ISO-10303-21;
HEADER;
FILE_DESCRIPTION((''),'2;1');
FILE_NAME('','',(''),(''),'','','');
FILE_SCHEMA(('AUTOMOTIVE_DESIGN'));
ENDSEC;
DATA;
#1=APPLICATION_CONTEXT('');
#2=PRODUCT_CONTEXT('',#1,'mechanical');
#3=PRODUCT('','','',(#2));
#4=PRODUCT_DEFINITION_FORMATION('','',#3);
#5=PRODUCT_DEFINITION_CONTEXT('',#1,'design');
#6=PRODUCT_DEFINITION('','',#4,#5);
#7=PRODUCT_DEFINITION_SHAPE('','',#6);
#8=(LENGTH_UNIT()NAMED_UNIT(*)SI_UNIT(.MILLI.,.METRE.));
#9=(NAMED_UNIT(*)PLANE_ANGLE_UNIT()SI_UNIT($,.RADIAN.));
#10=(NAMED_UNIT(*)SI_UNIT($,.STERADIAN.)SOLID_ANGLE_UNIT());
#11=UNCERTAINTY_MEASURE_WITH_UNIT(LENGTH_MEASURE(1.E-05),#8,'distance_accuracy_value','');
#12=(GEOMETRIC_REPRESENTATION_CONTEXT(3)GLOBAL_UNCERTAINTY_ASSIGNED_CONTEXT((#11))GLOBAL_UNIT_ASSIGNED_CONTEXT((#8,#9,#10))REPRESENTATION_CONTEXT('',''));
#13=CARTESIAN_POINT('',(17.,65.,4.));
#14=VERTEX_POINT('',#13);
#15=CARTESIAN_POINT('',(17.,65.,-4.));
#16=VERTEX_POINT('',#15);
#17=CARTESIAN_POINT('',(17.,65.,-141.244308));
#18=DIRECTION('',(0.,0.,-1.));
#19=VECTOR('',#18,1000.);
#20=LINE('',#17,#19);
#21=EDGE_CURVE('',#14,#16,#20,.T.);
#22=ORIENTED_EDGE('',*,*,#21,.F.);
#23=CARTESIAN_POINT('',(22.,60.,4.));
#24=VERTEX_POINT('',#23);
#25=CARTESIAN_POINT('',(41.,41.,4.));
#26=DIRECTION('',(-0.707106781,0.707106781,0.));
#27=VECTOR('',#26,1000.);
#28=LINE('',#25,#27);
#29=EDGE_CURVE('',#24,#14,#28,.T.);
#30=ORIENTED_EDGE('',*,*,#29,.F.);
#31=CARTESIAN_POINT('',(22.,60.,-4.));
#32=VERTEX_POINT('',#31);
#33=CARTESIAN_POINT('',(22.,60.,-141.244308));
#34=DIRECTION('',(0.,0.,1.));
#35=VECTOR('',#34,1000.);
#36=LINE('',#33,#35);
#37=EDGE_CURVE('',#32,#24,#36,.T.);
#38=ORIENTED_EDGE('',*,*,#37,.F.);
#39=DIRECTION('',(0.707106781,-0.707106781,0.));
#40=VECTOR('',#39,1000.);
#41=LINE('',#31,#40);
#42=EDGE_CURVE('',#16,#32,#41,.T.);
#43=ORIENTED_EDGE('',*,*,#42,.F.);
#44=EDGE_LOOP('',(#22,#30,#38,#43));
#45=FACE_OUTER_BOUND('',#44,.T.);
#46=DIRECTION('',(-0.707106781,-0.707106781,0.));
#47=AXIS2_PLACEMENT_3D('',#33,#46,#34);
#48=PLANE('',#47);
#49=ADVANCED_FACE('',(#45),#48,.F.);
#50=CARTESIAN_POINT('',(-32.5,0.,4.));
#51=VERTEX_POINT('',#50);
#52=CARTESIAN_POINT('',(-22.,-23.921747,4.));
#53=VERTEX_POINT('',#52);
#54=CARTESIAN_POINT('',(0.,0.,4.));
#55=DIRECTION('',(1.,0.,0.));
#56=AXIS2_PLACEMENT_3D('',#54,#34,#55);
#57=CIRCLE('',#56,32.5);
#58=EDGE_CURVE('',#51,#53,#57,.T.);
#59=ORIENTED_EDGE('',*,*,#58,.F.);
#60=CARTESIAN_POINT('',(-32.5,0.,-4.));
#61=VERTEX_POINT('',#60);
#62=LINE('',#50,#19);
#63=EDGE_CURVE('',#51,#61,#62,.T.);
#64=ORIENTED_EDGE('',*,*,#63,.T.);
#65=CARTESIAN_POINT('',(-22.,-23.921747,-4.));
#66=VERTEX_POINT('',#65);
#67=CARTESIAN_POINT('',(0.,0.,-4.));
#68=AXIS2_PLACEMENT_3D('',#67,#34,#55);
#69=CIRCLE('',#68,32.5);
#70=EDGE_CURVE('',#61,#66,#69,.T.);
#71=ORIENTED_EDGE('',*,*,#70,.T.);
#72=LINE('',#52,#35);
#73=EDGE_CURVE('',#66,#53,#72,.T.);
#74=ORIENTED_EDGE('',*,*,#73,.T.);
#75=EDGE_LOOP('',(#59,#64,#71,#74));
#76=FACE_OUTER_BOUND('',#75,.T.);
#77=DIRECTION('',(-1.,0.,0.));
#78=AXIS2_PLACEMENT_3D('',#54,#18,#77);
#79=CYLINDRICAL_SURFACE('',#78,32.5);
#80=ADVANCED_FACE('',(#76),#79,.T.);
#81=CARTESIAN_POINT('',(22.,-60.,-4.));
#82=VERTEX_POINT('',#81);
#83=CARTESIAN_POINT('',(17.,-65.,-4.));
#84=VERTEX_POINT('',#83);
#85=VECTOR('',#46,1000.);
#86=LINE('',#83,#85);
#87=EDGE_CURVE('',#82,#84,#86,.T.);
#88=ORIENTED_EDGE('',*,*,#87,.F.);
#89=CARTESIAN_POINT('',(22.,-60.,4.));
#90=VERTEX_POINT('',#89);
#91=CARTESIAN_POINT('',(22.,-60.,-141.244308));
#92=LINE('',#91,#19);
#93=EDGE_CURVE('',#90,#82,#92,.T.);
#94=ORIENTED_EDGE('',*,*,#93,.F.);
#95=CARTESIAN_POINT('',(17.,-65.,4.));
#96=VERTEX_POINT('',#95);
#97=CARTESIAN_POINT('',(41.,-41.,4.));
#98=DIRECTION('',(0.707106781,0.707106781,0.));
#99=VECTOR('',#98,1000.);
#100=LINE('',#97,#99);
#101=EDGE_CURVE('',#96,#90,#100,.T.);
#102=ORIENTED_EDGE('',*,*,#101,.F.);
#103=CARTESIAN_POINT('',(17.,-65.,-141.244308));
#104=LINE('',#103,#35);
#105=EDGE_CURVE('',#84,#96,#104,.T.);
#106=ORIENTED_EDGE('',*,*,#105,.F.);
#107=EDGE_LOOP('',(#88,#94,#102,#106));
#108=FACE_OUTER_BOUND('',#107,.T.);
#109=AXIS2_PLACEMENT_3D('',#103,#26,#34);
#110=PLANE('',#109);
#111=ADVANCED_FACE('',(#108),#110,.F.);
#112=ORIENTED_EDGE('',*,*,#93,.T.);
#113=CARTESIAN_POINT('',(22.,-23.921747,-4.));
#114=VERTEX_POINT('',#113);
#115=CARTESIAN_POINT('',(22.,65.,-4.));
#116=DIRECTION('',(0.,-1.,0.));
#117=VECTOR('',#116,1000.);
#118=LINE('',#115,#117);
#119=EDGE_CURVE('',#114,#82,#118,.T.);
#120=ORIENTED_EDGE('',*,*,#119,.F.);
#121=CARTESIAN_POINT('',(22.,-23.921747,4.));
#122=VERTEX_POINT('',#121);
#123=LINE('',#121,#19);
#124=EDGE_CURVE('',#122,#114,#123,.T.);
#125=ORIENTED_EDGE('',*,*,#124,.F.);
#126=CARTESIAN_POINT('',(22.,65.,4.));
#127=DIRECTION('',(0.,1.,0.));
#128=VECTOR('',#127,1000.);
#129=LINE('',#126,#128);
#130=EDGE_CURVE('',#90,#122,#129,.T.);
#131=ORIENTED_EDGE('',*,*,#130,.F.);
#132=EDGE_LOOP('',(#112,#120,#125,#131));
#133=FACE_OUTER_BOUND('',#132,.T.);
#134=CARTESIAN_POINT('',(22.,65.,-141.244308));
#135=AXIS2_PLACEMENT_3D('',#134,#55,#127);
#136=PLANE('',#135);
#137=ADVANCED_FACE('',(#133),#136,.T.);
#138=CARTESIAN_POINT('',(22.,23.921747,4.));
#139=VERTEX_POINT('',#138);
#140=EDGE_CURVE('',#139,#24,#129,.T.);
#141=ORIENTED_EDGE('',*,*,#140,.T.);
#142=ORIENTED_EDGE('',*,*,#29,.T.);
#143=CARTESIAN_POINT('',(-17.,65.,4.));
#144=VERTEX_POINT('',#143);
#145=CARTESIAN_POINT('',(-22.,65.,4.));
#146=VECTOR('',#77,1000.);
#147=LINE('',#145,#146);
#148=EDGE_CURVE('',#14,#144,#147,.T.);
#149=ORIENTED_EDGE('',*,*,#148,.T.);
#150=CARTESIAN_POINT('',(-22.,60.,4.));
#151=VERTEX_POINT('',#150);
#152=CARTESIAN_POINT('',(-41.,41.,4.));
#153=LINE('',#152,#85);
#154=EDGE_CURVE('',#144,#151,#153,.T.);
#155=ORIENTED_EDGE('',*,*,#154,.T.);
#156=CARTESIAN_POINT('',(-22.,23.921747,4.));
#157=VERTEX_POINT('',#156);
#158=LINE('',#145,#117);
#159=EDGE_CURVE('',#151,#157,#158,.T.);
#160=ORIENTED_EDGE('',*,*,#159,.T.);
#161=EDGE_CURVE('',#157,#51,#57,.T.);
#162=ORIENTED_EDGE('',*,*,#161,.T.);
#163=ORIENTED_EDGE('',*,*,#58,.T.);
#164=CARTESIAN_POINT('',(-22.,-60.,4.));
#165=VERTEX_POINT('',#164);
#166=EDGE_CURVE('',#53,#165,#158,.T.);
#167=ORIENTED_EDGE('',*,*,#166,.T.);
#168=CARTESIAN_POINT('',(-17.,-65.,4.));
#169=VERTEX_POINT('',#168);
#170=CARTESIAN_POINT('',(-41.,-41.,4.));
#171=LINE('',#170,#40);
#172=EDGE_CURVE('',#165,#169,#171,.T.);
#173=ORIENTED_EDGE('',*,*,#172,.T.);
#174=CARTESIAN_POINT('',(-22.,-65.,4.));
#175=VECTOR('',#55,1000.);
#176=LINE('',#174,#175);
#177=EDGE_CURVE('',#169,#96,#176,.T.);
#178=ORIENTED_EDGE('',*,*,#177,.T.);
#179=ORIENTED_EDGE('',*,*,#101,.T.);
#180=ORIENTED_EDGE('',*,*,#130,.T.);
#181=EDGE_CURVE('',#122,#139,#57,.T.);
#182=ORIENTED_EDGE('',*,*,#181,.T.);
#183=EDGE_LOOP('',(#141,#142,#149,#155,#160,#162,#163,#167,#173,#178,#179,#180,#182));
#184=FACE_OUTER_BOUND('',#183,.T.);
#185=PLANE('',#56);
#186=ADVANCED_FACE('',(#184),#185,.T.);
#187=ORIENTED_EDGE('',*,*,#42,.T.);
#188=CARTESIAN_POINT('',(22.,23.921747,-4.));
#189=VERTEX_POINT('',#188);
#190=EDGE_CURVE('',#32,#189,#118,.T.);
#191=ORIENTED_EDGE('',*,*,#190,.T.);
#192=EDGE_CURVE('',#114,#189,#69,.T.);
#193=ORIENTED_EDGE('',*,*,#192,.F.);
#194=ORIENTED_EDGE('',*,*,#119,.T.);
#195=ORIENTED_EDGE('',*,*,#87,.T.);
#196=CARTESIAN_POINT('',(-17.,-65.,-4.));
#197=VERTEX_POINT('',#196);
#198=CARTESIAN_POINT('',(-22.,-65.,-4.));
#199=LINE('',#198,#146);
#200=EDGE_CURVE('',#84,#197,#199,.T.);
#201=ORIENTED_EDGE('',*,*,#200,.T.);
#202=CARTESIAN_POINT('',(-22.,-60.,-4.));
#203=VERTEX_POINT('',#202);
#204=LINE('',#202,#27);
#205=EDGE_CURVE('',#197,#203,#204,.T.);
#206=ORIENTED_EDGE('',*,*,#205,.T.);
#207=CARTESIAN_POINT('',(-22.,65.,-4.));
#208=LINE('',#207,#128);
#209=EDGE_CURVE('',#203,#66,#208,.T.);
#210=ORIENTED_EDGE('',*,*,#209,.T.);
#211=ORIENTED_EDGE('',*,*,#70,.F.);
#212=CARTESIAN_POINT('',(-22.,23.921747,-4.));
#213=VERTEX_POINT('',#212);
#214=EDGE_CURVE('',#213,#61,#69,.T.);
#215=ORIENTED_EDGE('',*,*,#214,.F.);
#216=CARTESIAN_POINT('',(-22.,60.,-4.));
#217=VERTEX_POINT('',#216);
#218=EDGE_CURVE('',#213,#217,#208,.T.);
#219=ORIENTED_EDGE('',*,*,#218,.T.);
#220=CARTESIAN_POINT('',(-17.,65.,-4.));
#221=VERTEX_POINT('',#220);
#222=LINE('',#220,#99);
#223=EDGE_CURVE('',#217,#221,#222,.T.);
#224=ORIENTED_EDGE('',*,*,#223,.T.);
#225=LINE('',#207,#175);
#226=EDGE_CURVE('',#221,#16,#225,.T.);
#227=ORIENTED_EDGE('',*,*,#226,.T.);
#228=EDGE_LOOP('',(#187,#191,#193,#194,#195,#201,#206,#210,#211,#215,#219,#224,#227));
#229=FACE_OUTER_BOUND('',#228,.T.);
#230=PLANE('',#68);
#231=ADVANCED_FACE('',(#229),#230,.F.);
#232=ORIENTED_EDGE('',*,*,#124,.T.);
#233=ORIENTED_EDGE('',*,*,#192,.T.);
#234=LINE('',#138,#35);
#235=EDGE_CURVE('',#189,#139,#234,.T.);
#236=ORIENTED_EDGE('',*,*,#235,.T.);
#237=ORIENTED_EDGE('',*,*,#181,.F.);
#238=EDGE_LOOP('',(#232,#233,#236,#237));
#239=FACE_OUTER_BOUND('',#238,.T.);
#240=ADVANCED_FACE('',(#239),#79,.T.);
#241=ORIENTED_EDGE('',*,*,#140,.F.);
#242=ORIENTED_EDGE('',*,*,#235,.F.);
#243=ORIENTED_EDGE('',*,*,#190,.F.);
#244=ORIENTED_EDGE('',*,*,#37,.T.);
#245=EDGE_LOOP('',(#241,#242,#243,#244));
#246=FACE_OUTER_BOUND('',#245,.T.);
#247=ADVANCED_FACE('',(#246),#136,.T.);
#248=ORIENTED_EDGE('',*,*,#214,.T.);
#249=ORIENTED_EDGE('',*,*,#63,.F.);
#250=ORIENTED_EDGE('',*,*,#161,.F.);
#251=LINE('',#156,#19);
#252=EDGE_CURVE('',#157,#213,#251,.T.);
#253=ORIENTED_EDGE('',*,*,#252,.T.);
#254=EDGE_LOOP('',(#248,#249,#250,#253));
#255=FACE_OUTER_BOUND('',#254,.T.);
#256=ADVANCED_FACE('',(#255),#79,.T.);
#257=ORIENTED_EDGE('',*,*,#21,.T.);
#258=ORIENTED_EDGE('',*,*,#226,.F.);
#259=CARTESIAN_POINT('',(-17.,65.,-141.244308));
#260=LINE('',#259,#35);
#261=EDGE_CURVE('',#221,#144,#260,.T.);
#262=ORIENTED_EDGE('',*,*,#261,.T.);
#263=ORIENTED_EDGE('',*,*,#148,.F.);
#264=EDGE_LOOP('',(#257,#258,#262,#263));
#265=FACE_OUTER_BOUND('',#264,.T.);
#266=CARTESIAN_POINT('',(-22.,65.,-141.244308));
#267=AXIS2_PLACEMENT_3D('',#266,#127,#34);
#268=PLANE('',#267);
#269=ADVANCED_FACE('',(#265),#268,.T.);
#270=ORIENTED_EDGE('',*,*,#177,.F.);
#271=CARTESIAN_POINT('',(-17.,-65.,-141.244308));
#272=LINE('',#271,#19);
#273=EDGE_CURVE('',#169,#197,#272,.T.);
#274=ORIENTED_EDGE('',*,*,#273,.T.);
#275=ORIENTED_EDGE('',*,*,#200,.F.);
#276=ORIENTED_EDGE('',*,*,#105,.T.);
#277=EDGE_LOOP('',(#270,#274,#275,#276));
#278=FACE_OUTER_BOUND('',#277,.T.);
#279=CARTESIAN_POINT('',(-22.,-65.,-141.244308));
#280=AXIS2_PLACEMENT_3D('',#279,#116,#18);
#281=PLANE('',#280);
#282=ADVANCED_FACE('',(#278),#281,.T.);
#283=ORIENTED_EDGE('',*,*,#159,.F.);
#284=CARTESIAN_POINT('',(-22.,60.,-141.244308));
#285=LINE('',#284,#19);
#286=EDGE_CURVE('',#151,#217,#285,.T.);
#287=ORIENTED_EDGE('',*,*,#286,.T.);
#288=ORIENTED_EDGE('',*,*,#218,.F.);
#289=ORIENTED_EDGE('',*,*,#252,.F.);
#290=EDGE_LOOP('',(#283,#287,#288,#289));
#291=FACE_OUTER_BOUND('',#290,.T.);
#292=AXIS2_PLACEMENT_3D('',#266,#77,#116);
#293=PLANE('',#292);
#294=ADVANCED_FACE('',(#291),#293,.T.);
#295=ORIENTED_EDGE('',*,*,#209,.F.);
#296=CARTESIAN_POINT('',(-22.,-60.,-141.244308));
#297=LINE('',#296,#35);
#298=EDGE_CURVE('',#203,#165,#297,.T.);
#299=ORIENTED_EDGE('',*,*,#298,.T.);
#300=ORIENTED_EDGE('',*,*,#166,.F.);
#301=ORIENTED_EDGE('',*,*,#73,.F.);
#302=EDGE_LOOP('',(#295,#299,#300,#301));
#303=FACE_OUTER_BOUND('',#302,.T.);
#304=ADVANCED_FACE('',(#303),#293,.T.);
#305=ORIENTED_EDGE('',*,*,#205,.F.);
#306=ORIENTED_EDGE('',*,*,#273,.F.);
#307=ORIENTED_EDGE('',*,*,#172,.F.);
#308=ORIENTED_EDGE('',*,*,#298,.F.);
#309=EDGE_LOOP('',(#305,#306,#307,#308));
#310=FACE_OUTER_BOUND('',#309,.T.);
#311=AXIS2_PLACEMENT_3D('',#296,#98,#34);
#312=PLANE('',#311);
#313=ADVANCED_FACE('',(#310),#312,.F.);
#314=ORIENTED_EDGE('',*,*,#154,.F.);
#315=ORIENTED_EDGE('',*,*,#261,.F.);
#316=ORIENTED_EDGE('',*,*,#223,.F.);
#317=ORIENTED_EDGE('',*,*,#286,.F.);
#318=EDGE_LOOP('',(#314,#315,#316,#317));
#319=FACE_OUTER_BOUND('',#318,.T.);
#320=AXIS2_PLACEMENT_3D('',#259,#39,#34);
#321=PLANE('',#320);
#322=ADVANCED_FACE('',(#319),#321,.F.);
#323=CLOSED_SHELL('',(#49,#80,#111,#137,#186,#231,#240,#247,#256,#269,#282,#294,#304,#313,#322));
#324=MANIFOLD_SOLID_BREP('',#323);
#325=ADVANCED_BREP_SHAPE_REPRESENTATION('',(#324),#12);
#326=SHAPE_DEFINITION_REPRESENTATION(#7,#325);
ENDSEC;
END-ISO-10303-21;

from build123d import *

# Parameters (mm, degrees)
SKETCH_1_R      = 32.5
EXTRUDE_1_DEPTH = 4
SKETCH_2_W      = 44
SKETCH_2_H      = 130
EXTRUDE_2_DEPTH = 8
CHAMFER_1_SIZE  = 5


with BuildPart() as part:
    # 草图1 → 凸台-拉伸1 (new, symmetric)
    with BuildSketch(Plane.XY):
        Circle(SKETCH_1_R)
    extrude(amount=EXTRUDE_1_DEPTH, both=True)

    # 草图2 → 凸台-拉伸2 (add)
    with BuildSketch(Plane.XY.offset(4)):
        Rectangle(SKETCH_2_W, SKETCH_2_H)
    extrude(amount=-EXTRUDE_2_DEPTH)

    # 倒角1
    chamfer_1_edges = [part.edges().sort_by_distance(p)[0] for p in [
        (22, 65, 0),
        (-22, -65, 0),
        (22, -65, 0),
        (-22, 65, 0),
    ]]
    chamfer(chamfer_1_edges, length=CHAMFER_1_SIZE)


solid = part.part
